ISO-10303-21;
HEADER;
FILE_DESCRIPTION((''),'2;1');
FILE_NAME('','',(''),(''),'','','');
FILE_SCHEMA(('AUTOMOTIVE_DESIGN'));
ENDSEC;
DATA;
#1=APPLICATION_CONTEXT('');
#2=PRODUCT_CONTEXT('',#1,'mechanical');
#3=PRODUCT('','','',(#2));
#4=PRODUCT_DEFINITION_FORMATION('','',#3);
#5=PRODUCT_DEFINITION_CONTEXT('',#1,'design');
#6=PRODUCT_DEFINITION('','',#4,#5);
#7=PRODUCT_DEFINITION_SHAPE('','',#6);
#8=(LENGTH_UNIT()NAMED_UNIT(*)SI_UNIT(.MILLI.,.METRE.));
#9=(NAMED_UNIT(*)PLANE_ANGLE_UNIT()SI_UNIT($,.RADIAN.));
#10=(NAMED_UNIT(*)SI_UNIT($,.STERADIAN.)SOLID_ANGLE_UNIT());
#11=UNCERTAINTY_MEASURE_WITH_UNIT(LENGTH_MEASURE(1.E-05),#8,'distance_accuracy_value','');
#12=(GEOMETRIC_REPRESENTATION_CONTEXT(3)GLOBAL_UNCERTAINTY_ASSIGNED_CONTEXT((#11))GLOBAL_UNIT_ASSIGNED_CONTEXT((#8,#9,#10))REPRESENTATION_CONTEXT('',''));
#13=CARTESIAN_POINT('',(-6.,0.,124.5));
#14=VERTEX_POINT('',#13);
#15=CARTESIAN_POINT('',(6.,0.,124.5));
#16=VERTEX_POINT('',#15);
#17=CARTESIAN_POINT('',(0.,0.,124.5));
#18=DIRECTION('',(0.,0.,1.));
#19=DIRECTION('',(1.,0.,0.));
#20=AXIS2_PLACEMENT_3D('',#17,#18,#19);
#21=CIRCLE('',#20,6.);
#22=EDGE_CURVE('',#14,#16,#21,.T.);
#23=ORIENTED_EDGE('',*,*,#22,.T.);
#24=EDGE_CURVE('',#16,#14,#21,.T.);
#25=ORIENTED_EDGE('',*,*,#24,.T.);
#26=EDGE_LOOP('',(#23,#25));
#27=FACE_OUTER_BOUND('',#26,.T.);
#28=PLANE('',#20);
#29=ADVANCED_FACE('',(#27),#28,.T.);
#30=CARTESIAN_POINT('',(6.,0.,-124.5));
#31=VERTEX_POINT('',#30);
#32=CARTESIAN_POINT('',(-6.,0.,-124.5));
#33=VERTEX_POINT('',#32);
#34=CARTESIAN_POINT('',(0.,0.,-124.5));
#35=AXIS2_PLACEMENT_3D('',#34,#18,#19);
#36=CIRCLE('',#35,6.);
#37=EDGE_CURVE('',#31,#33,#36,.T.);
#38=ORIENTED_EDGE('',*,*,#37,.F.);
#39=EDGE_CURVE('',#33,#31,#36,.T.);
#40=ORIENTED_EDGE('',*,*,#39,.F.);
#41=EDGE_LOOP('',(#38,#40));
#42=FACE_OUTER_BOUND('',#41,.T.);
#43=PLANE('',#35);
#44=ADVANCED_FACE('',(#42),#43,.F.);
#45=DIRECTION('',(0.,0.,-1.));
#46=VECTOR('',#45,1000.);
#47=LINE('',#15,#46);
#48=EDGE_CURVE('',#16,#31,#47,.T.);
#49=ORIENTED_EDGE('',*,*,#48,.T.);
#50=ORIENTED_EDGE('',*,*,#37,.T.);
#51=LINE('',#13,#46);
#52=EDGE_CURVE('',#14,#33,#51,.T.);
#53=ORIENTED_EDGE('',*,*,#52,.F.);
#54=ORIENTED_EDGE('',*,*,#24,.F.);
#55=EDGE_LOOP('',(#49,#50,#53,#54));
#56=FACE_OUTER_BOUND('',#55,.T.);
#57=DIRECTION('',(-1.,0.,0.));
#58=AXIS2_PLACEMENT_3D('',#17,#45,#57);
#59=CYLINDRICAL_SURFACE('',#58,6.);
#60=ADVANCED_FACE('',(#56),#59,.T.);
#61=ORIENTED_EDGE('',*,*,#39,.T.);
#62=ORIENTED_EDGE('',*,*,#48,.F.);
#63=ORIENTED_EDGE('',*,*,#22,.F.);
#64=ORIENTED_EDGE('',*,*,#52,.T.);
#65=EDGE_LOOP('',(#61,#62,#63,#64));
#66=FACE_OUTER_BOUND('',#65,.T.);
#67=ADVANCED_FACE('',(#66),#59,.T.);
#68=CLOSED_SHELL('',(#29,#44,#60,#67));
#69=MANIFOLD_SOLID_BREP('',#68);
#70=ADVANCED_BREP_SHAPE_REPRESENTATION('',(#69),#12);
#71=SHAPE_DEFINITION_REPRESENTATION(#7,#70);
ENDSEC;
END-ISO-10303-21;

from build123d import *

# Parameters (mm, degrees)
SKETCH1_R           = 6
BOSS_EXTRUDE1_DEPTH = 124.5


with BuildPart() as part:
    # Sketch1 → Boss-Extrude1 (new, symmetric)
    with BuildSketch(Plane.XY):
        Circle(SKETCH1_R)
    extrude(amount=BOSS_EXTRUDE1_DEPTH, both=True)


solid = part.part
